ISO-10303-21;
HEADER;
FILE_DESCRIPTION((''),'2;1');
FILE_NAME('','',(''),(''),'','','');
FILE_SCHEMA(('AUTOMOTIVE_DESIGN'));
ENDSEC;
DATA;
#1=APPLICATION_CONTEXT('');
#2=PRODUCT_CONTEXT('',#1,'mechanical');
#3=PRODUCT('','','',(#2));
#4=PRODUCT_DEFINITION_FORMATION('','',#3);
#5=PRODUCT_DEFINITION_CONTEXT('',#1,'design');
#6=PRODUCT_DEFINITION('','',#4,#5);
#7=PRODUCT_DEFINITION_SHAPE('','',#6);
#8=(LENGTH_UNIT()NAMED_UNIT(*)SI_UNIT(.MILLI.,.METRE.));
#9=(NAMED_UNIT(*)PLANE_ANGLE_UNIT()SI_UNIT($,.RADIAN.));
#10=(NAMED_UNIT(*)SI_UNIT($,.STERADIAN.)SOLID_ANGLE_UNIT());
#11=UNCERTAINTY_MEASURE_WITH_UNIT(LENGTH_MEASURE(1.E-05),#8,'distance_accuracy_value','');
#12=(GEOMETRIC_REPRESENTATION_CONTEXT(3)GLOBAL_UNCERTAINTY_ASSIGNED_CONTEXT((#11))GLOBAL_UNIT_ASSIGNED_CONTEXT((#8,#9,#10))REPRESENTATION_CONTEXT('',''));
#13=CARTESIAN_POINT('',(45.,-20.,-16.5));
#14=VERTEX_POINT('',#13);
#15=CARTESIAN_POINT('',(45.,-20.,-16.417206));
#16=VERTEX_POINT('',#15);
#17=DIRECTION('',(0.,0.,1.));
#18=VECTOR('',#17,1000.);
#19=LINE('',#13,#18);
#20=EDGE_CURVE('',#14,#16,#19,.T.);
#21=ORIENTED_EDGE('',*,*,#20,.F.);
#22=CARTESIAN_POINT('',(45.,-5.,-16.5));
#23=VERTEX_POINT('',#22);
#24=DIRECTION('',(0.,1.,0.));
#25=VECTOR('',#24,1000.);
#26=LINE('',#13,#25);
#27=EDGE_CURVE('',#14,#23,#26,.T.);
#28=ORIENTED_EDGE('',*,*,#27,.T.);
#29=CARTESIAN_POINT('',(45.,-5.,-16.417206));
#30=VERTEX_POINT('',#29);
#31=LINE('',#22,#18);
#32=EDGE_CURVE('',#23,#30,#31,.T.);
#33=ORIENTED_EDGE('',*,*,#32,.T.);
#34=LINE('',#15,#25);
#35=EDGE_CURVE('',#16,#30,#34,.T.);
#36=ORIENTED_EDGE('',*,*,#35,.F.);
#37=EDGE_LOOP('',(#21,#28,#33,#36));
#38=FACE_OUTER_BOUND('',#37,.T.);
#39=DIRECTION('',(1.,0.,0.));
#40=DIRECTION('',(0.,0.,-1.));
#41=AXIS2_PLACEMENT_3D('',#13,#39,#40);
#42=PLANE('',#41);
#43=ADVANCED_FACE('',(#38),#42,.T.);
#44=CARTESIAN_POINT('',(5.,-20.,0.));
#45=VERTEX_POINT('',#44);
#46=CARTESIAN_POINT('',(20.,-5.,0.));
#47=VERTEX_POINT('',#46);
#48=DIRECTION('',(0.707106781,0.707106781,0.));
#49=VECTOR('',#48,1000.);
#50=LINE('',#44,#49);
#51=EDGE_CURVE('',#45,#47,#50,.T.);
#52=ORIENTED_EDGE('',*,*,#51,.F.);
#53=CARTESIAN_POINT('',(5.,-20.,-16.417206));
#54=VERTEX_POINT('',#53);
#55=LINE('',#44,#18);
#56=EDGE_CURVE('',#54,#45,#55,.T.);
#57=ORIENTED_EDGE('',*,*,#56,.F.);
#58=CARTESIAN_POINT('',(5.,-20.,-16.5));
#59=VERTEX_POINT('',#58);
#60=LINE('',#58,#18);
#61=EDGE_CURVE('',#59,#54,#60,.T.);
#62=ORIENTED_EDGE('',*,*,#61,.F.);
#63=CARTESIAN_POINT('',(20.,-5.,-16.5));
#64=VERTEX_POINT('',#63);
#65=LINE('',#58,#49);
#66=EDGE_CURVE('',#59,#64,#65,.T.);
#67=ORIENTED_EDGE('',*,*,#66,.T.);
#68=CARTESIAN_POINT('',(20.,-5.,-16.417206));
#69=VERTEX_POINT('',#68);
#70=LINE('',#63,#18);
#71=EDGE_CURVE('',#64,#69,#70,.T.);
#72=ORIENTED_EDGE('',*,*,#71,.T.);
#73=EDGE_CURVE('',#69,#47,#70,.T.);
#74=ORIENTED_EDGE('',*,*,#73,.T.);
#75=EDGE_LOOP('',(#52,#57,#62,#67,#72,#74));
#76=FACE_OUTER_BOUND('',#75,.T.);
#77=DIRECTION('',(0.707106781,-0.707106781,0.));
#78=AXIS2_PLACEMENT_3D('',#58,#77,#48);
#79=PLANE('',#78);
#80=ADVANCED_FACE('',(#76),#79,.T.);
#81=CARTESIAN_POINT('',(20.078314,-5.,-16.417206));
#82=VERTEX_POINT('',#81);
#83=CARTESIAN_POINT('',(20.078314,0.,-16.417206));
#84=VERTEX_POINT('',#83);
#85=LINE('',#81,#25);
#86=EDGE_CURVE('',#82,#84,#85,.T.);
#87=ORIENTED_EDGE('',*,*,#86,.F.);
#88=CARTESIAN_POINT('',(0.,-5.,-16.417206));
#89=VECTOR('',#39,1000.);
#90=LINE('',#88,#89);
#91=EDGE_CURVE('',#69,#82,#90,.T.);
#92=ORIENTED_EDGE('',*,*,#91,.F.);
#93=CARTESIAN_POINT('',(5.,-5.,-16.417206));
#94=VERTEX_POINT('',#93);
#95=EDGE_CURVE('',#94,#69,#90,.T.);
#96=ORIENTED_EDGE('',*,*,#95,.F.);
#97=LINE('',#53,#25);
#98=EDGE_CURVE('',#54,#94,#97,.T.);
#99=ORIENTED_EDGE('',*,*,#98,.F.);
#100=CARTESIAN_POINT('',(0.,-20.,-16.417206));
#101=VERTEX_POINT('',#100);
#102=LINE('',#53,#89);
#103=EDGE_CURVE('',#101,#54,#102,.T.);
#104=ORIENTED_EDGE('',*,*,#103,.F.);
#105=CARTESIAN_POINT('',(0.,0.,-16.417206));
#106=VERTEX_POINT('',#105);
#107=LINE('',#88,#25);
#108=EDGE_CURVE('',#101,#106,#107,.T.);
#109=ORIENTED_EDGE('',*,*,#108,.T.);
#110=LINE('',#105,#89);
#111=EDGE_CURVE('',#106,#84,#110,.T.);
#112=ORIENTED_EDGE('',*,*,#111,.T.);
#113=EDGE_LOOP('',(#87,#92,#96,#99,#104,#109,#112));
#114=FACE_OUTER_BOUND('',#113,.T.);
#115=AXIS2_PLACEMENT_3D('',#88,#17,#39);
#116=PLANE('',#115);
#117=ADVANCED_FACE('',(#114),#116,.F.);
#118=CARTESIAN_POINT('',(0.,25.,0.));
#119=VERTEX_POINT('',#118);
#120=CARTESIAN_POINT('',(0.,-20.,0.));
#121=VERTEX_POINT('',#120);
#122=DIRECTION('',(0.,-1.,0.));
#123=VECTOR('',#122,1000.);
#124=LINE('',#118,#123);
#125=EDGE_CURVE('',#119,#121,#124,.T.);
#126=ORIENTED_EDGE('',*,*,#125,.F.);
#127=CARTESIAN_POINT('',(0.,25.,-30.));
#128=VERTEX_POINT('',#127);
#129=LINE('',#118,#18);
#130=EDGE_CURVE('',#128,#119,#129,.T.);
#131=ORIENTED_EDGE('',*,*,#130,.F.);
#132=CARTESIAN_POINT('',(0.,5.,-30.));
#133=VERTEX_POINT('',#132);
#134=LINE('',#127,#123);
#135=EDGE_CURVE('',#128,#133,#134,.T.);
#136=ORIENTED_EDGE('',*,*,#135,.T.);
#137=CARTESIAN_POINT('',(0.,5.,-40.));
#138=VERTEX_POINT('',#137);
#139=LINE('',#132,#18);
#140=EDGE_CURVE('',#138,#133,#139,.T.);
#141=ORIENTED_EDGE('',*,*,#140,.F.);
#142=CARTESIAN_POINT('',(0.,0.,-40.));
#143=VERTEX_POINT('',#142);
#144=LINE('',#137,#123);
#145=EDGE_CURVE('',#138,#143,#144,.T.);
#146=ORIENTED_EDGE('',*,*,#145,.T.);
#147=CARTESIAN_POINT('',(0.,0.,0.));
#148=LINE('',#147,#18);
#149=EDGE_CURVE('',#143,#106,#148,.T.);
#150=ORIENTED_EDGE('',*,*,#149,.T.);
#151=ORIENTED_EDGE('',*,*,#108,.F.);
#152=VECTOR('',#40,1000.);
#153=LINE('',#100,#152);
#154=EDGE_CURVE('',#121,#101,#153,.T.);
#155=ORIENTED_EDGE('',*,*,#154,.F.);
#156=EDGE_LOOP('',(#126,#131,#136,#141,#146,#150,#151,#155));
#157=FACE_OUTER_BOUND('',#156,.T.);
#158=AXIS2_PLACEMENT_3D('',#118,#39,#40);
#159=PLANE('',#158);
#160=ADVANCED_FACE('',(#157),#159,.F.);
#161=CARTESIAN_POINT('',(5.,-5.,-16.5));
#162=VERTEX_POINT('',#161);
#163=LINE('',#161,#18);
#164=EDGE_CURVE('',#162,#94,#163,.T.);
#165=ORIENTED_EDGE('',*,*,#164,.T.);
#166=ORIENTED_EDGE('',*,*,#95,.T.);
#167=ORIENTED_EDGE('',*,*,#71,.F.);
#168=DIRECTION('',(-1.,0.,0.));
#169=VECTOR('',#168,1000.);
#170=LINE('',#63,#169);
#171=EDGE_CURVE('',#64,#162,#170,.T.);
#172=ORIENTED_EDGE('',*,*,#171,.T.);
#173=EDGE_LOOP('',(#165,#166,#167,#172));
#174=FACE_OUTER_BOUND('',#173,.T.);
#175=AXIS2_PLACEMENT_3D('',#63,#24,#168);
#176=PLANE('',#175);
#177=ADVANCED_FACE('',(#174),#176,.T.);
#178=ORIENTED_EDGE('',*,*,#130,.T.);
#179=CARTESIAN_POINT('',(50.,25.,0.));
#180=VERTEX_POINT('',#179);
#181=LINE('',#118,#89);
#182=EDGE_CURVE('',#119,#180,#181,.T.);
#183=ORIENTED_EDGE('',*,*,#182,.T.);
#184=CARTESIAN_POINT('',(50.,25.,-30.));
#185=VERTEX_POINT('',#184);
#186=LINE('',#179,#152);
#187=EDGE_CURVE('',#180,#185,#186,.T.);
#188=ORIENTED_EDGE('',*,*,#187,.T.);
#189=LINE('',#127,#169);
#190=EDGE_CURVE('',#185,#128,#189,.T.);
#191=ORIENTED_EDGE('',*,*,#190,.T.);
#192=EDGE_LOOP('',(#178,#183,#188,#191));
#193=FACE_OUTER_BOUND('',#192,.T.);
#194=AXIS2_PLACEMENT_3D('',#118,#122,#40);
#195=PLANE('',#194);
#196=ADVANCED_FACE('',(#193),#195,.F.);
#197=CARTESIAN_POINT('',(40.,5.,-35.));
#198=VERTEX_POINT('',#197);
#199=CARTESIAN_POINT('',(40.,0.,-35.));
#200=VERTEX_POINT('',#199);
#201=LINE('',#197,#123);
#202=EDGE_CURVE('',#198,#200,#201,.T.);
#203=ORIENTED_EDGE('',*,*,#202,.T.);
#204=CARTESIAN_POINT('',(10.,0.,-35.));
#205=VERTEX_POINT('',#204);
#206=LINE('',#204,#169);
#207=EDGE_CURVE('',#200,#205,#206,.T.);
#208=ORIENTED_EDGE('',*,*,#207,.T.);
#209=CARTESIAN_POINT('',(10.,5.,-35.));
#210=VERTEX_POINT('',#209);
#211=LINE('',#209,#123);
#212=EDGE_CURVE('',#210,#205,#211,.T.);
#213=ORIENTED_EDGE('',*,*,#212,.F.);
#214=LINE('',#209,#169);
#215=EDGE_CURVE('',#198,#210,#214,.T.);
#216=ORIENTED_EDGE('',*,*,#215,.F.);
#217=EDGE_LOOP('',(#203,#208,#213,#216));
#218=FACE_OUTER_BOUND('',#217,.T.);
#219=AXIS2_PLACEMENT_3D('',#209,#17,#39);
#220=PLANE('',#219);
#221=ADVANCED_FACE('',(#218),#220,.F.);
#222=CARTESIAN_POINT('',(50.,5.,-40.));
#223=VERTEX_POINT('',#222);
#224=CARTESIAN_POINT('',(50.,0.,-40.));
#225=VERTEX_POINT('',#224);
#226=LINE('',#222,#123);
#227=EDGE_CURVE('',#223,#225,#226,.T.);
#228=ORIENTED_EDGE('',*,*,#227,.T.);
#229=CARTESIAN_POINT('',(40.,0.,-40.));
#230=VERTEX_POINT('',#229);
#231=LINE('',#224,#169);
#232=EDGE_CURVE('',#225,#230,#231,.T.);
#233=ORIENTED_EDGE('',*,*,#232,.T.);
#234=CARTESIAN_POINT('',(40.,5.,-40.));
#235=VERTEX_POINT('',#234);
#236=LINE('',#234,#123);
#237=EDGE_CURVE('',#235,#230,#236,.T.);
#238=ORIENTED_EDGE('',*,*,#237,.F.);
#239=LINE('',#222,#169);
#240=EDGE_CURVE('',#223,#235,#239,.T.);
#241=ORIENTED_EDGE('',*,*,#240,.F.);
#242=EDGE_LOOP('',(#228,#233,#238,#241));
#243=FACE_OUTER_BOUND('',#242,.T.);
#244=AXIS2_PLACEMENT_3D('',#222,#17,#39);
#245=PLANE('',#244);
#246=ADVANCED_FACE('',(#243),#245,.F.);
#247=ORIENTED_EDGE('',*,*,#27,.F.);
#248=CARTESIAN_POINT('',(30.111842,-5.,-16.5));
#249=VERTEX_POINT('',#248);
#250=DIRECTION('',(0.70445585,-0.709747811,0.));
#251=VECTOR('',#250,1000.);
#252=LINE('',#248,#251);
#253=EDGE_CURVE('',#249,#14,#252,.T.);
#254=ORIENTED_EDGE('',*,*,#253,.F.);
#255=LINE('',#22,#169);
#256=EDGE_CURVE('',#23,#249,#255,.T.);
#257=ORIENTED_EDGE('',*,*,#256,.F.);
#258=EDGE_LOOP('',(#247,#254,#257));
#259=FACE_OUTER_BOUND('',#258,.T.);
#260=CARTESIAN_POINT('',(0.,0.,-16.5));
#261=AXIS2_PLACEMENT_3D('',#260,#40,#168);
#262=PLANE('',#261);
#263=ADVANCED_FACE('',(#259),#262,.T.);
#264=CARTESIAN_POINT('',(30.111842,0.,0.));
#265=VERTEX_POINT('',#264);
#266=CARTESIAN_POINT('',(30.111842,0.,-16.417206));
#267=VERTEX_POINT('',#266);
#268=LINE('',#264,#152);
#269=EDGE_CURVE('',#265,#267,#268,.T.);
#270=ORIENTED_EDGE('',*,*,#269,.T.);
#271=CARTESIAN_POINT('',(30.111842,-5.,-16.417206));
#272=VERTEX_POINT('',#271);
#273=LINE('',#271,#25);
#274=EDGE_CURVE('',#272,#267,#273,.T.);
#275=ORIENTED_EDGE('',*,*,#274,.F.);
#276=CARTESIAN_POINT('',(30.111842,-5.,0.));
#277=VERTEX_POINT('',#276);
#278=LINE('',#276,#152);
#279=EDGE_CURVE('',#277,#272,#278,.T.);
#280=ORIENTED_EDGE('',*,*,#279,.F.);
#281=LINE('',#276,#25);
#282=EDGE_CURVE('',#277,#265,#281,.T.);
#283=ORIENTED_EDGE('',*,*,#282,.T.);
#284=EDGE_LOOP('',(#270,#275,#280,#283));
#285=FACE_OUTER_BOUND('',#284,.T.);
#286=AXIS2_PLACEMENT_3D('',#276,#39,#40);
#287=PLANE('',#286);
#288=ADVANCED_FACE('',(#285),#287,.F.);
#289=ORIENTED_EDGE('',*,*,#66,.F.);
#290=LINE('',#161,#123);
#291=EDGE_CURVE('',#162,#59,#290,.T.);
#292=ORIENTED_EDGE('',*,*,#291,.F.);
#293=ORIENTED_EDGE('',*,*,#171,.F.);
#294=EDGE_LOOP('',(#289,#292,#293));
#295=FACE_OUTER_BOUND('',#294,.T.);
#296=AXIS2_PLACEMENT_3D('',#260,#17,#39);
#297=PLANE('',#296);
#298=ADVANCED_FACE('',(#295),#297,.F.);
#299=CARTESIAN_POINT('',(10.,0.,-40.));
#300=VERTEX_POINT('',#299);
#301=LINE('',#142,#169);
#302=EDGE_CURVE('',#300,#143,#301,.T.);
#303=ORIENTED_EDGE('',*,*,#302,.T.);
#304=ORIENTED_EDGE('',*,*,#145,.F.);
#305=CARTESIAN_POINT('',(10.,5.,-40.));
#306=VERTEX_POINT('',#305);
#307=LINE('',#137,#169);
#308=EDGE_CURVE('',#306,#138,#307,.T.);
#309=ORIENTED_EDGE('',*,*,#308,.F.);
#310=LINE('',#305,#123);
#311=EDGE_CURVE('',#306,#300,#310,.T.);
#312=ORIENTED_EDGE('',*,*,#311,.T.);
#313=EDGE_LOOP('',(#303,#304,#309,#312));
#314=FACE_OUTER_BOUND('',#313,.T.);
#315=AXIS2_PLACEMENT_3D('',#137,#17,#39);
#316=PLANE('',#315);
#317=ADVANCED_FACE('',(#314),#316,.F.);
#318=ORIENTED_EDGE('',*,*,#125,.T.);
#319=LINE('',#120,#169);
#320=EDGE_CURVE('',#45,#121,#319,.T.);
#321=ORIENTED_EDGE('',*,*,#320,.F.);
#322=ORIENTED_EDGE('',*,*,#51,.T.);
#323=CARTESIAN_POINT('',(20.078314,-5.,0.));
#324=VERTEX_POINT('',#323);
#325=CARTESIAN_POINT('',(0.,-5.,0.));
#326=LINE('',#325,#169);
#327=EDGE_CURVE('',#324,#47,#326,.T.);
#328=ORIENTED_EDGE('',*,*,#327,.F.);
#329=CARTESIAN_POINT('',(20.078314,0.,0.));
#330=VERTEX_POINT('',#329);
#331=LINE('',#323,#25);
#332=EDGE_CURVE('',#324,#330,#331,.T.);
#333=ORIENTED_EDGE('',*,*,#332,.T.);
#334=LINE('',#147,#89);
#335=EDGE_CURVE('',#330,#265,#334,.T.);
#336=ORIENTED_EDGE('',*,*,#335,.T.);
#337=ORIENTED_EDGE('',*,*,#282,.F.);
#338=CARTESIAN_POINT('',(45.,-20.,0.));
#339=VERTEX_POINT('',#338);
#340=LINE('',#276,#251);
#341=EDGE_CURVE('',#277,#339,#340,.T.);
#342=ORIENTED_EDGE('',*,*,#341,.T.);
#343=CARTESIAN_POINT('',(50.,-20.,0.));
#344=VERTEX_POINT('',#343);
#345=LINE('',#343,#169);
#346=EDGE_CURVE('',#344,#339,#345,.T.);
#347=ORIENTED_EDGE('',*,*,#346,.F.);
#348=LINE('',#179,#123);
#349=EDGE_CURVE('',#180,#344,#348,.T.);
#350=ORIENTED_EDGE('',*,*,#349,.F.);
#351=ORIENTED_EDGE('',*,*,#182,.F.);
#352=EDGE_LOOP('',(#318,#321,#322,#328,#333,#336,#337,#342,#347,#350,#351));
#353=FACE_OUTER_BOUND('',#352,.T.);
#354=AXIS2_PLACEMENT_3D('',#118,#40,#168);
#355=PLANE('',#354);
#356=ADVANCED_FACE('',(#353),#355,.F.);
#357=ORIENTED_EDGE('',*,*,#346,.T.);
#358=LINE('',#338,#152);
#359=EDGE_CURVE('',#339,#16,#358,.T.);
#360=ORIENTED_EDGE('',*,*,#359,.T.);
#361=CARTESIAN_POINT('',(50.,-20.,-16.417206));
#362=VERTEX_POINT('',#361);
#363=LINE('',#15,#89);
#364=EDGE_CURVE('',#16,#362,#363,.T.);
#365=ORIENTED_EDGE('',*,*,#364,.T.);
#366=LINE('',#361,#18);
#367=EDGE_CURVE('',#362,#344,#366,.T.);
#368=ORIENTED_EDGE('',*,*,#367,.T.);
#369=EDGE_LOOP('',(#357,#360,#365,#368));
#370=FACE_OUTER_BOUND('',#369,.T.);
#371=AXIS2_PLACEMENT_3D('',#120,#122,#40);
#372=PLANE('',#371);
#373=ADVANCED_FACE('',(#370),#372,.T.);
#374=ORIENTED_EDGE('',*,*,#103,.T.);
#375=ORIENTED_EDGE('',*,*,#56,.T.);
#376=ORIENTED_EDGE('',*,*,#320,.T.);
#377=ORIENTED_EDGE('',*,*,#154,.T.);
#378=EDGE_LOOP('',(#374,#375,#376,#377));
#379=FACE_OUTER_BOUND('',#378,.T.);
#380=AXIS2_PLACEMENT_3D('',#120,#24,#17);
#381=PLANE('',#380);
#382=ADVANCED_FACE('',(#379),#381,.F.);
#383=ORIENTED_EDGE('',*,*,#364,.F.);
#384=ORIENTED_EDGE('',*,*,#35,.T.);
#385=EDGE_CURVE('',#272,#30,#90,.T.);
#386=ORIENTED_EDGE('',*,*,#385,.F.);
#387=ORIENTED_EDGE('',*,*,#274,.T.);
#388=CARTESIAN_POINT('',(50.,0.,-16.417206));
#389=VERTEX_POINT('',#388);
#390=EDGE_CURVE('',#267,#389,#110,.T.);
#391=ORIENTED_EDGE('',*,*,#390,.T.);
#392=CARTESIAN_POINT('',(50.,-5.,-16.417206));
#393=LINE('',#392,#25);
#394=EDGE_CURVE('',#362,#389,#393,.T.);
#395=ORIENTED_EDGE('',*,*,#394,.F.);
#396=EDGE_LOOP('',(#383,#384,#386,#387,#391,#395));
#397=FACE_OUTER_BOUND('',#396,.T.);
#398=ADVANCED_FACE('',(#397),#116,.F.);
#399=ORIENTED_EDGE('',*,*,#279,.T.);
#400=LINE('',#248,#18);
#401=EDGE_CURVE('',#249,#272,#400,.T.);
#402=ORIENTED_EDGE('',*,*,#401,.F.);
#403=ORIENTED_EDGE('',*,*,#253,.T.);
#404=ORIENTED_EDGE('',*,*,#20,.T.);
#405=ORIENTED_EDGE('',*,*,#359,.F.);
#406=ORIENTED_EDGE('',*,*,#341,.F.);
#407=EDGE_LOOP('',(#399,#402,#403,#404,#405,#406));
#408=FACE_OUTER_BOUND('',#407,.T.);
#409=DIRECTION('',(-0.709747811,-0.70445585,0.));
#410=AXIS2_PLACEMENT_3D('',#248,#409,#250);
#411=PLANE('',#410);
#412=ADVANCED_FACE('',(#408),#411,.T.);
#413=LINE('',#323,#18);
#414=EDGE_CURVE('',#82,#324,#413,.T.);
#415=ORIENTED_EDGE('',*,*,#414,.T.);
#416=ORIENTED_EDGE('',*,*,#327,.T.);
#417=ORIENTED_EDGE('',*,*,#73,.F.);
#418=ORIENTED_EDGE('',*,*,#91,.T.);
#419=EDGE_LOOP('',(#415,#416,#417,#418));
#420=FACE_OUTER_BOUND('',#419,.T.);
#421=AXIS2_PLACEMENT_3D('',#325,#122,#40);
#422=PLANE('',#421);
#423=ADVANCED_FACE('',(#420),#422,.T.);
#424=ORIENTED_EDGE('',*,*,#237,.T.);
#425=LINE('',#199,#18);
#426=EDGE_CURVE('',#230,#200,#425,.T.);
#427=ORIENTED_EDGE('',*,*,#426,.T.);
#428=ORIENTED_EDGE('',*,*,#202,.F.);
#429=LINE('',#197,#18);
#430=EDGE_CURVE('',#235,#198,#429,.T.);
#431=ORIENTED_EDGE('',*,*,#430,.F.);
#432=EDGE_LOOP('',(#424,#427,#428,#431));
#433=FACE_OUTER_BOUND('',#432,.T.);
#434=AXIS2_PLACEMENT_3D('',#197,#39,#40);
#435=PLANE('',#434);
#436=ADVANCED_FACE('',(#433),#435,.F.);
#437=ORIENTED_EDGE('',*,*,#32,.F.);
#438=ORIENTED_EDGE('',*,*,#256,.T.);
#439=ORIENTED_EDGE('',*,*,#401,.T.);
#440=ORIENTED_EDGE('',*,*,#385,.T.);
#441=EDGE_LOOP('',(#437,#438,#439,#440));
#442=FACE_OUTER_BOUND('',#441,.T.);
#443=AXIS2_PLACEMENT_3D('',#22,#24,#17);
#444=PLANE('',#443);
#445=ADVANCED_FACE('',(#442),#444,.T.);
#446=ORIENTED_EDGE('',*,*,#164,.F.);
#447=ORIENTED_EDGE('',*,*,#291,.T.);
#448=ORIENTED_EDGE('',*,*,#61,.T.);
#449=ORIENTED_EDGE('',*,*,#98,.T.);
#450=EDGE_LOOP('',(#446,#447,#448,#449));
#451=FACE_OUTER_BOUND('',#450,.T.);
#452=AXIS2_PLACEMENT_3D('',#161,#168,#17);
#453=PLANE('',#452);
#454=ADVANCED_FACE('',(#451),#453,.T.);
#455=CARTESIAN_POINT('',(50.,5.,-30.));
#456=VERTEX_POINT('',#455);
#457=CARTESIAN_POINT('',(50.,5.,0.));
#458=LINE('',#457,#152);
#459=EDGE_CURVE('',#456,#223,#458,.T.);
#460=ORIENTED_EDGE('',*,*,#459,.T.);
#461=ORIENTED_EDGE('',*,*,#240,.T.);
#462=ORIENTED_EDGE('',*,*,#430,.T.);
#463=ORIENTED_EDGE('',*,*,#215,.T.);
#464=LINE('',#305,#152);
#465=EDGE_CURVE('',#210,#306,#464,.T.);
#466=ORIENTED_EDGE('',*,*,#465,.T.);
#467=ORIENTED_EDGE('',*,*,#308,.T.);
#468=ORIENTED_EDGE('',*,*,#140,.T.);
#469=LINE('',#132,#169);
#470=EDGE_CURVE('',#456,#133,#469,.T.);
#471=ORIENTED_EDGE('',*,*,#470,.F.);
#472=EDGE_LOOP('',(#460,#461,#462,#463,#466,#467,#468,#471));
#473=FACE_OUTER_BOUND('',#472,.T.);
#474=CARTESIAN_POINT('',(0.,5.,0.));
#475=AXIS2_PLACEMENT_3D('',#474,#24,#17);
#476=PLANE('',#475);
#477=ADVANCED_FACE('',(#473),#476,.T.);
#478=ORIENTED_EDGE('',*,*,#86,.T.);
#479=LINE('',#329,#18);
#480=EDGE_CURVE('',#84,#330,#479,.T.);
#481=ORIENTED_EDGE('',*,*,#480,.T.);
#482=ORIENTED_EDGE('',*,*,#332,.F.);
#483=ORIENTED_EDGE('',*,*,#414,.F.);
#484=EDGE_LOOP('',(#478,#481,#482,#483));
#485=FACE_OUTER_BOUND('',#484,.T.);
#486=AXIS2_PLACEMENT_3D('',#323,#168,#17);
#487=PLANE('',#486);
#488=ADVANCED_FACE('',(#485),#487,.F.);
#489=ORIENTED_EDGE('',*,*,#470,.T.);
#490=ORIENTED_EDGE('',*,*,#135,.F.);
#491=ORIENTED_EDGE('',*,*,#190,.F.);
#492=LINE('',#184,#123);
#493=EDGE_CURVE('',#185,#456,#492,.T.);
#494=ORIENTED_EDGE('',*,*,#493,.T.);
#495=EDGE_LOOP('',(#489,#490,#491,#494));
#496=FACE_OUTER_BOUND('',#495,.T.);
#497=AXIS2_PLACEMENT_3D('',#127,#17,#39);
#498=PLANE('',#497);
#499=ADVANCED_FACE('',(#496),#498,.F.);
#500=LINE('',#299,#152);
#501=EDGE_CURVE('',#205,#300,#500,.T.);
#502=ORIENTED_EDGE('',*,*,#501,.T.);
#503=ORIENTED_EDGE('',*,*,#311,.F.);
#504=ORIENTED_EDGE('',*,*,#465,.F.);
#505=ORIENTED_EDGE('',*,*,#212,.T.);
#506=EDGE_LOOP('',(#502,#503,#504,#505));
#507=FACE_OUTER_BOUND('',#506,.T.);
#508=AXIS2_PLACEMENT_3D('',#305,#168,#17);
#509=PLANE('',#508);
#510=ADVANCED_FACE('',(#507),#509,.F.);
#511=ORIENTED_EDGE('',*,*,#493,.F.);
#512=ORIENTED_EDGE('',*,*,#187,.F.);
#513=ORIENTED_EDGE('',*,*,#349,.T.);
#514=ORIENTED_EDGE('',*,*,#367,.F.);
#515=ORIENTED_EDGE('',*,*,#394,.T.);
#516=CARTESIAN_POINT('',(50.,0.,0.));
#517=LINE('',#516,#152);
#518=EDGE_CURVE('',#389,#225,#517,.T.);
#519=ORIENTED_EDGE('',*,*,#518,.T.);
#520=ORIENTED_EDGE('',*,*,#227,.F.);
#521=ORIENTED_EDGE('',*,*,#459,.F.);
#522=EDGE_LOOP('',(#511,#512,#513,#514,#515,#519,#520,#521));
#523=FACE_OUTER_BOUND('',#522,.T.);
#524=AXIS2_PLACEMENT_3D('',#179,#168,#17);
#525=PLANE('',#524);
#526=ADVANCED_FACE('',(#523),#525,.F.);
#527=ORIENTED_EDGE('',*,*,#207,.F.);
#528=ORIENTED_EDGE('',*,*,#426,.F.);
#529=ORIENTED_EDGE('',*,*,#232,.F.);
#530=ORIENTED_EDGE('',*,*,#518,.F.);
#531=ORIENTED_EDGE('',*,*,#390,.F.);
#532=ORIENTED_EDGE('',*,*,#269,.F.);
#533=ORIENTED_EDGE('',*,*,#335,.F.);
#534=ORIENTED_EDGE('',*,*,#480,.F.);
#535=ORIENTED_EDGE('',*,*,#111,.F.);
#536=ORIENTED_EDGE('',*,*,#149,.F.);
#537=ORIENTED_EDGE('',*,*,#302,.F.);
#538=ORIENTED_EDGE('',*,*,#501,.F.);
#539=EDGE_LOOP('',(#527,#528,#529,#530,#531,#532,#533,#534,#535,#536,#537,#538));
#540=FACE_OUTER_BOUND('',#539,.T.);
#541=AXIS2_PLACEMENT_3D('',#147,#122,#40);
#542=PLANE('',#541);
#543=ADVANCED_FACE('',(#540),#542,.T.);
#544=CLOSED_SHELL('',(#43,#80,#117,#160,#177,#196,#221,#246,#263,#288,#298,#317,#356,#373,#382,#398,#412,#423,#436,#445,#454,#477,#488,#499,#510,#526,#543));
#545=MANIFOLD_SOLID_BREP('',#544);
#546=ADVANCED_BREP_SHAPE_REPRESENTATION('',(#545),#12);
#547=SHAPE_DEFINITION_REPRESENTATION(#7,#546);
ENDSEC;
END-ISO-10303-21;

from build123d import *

# Parameters (mm, degrees)
BASE_BLOCK_SKETCH_W       = 50
BASE_BLOCK_SKETCH_H       = 30
BASE_BLOCK_50X30X25_DEPTH = 25
CORNER_STEP_5MM_DEPTH     = 5
LOWER_PLATE_SKETCH_W      = 19.888158271
LOWER_PLATE_SKETCH_H      = 16.417205811
LOWER_PLATE_5MM_DEPTH     = 5
LEG_SKETCH_W              = 5
LEG_SKETCH_H              = 16.417205811
LEG_15MM_DEPTH            = 15
TAPERED_WEB_16_5MM_DEPTH  = 16.5


with BuildPart() as part:
    # Base Block Sketch → Base Block 50x30x25 (new body)
    with BuildSketch(Plane(origin=(0, 0, 0), x_dir=(1, 0, 0), z_dir=(0, 1, 0))):
        with Locations((25, 15)):
            Rectangle(BASE_BLOCK_SKETCH_W, BASE_BLOCK_SKETCH_H)
    extrude(amount=BASE_BLOCK_50X30X25_DEPTH)

    # Corner Step Sketch → Corner Step 5mm (add)
    with BuildSketch(Plane(origin=(0, 0, 0), x_dir=(1, 0, 0), z_dir=(0, 1, 0))):
        Polygon((0, 30), (0, 40), (10, 40), (10, 35), (40, 35), (40, 40), (50, 40), (50, 30), (50, 0), (0, 0), align=None)
    extrude(amount=CORNER_STEP_5MM_DEPTH)

    # Lower Plate Sketch → Lower Plate 5mm (add)
    with BuildSketch(Plane.XZ):
        Polygon((6.770734002, 0), (0, 0), (0, -16.417205811), (6.770734002, -16.417205811), (20.078313967, -16.417205811), (20.078313967, 0), align=None)
        with Locations((40.055920865, -8.208602906)):
            Rectangle(LOWER_PLATE_SKETCH_W, LOWER_PLATE_SKETCH_H)
    extrude(amount=LOWER_PLATE_5MM_DEPTH)

    # Leg Sketch → Leg 15mm (add)
    with BuildSketch(Plane(origin=(0, -5, 0), x_dir=(-1, 0, 0), z_dir=(0, -1, 0))):
        with Locations((-2.5, 8.208602906)):
            Rectangle(LEG_SKETCH_W, LEG_SKETCH_H)
        with Locations((-47.5, 8.208602906)):
            Rectangle(LEG_SKETCH_W, LEG_SKETCH_H)
    extrude(amount=LEG_15MM_DEPTH)

    # Tapered Web Sketch → Tapered Web 16.5mm (add)
    with BuildSketch(Plane.XY):
        Polygon((30.111841729, -5), (45, -20), (45, -5), align=None)
        Polygon((5, -5), (5, -20), (20, -5), align=None)
    extrude(amount=-TAPERED_WEB_16_5MM_DEPTH)


solid = part.part
